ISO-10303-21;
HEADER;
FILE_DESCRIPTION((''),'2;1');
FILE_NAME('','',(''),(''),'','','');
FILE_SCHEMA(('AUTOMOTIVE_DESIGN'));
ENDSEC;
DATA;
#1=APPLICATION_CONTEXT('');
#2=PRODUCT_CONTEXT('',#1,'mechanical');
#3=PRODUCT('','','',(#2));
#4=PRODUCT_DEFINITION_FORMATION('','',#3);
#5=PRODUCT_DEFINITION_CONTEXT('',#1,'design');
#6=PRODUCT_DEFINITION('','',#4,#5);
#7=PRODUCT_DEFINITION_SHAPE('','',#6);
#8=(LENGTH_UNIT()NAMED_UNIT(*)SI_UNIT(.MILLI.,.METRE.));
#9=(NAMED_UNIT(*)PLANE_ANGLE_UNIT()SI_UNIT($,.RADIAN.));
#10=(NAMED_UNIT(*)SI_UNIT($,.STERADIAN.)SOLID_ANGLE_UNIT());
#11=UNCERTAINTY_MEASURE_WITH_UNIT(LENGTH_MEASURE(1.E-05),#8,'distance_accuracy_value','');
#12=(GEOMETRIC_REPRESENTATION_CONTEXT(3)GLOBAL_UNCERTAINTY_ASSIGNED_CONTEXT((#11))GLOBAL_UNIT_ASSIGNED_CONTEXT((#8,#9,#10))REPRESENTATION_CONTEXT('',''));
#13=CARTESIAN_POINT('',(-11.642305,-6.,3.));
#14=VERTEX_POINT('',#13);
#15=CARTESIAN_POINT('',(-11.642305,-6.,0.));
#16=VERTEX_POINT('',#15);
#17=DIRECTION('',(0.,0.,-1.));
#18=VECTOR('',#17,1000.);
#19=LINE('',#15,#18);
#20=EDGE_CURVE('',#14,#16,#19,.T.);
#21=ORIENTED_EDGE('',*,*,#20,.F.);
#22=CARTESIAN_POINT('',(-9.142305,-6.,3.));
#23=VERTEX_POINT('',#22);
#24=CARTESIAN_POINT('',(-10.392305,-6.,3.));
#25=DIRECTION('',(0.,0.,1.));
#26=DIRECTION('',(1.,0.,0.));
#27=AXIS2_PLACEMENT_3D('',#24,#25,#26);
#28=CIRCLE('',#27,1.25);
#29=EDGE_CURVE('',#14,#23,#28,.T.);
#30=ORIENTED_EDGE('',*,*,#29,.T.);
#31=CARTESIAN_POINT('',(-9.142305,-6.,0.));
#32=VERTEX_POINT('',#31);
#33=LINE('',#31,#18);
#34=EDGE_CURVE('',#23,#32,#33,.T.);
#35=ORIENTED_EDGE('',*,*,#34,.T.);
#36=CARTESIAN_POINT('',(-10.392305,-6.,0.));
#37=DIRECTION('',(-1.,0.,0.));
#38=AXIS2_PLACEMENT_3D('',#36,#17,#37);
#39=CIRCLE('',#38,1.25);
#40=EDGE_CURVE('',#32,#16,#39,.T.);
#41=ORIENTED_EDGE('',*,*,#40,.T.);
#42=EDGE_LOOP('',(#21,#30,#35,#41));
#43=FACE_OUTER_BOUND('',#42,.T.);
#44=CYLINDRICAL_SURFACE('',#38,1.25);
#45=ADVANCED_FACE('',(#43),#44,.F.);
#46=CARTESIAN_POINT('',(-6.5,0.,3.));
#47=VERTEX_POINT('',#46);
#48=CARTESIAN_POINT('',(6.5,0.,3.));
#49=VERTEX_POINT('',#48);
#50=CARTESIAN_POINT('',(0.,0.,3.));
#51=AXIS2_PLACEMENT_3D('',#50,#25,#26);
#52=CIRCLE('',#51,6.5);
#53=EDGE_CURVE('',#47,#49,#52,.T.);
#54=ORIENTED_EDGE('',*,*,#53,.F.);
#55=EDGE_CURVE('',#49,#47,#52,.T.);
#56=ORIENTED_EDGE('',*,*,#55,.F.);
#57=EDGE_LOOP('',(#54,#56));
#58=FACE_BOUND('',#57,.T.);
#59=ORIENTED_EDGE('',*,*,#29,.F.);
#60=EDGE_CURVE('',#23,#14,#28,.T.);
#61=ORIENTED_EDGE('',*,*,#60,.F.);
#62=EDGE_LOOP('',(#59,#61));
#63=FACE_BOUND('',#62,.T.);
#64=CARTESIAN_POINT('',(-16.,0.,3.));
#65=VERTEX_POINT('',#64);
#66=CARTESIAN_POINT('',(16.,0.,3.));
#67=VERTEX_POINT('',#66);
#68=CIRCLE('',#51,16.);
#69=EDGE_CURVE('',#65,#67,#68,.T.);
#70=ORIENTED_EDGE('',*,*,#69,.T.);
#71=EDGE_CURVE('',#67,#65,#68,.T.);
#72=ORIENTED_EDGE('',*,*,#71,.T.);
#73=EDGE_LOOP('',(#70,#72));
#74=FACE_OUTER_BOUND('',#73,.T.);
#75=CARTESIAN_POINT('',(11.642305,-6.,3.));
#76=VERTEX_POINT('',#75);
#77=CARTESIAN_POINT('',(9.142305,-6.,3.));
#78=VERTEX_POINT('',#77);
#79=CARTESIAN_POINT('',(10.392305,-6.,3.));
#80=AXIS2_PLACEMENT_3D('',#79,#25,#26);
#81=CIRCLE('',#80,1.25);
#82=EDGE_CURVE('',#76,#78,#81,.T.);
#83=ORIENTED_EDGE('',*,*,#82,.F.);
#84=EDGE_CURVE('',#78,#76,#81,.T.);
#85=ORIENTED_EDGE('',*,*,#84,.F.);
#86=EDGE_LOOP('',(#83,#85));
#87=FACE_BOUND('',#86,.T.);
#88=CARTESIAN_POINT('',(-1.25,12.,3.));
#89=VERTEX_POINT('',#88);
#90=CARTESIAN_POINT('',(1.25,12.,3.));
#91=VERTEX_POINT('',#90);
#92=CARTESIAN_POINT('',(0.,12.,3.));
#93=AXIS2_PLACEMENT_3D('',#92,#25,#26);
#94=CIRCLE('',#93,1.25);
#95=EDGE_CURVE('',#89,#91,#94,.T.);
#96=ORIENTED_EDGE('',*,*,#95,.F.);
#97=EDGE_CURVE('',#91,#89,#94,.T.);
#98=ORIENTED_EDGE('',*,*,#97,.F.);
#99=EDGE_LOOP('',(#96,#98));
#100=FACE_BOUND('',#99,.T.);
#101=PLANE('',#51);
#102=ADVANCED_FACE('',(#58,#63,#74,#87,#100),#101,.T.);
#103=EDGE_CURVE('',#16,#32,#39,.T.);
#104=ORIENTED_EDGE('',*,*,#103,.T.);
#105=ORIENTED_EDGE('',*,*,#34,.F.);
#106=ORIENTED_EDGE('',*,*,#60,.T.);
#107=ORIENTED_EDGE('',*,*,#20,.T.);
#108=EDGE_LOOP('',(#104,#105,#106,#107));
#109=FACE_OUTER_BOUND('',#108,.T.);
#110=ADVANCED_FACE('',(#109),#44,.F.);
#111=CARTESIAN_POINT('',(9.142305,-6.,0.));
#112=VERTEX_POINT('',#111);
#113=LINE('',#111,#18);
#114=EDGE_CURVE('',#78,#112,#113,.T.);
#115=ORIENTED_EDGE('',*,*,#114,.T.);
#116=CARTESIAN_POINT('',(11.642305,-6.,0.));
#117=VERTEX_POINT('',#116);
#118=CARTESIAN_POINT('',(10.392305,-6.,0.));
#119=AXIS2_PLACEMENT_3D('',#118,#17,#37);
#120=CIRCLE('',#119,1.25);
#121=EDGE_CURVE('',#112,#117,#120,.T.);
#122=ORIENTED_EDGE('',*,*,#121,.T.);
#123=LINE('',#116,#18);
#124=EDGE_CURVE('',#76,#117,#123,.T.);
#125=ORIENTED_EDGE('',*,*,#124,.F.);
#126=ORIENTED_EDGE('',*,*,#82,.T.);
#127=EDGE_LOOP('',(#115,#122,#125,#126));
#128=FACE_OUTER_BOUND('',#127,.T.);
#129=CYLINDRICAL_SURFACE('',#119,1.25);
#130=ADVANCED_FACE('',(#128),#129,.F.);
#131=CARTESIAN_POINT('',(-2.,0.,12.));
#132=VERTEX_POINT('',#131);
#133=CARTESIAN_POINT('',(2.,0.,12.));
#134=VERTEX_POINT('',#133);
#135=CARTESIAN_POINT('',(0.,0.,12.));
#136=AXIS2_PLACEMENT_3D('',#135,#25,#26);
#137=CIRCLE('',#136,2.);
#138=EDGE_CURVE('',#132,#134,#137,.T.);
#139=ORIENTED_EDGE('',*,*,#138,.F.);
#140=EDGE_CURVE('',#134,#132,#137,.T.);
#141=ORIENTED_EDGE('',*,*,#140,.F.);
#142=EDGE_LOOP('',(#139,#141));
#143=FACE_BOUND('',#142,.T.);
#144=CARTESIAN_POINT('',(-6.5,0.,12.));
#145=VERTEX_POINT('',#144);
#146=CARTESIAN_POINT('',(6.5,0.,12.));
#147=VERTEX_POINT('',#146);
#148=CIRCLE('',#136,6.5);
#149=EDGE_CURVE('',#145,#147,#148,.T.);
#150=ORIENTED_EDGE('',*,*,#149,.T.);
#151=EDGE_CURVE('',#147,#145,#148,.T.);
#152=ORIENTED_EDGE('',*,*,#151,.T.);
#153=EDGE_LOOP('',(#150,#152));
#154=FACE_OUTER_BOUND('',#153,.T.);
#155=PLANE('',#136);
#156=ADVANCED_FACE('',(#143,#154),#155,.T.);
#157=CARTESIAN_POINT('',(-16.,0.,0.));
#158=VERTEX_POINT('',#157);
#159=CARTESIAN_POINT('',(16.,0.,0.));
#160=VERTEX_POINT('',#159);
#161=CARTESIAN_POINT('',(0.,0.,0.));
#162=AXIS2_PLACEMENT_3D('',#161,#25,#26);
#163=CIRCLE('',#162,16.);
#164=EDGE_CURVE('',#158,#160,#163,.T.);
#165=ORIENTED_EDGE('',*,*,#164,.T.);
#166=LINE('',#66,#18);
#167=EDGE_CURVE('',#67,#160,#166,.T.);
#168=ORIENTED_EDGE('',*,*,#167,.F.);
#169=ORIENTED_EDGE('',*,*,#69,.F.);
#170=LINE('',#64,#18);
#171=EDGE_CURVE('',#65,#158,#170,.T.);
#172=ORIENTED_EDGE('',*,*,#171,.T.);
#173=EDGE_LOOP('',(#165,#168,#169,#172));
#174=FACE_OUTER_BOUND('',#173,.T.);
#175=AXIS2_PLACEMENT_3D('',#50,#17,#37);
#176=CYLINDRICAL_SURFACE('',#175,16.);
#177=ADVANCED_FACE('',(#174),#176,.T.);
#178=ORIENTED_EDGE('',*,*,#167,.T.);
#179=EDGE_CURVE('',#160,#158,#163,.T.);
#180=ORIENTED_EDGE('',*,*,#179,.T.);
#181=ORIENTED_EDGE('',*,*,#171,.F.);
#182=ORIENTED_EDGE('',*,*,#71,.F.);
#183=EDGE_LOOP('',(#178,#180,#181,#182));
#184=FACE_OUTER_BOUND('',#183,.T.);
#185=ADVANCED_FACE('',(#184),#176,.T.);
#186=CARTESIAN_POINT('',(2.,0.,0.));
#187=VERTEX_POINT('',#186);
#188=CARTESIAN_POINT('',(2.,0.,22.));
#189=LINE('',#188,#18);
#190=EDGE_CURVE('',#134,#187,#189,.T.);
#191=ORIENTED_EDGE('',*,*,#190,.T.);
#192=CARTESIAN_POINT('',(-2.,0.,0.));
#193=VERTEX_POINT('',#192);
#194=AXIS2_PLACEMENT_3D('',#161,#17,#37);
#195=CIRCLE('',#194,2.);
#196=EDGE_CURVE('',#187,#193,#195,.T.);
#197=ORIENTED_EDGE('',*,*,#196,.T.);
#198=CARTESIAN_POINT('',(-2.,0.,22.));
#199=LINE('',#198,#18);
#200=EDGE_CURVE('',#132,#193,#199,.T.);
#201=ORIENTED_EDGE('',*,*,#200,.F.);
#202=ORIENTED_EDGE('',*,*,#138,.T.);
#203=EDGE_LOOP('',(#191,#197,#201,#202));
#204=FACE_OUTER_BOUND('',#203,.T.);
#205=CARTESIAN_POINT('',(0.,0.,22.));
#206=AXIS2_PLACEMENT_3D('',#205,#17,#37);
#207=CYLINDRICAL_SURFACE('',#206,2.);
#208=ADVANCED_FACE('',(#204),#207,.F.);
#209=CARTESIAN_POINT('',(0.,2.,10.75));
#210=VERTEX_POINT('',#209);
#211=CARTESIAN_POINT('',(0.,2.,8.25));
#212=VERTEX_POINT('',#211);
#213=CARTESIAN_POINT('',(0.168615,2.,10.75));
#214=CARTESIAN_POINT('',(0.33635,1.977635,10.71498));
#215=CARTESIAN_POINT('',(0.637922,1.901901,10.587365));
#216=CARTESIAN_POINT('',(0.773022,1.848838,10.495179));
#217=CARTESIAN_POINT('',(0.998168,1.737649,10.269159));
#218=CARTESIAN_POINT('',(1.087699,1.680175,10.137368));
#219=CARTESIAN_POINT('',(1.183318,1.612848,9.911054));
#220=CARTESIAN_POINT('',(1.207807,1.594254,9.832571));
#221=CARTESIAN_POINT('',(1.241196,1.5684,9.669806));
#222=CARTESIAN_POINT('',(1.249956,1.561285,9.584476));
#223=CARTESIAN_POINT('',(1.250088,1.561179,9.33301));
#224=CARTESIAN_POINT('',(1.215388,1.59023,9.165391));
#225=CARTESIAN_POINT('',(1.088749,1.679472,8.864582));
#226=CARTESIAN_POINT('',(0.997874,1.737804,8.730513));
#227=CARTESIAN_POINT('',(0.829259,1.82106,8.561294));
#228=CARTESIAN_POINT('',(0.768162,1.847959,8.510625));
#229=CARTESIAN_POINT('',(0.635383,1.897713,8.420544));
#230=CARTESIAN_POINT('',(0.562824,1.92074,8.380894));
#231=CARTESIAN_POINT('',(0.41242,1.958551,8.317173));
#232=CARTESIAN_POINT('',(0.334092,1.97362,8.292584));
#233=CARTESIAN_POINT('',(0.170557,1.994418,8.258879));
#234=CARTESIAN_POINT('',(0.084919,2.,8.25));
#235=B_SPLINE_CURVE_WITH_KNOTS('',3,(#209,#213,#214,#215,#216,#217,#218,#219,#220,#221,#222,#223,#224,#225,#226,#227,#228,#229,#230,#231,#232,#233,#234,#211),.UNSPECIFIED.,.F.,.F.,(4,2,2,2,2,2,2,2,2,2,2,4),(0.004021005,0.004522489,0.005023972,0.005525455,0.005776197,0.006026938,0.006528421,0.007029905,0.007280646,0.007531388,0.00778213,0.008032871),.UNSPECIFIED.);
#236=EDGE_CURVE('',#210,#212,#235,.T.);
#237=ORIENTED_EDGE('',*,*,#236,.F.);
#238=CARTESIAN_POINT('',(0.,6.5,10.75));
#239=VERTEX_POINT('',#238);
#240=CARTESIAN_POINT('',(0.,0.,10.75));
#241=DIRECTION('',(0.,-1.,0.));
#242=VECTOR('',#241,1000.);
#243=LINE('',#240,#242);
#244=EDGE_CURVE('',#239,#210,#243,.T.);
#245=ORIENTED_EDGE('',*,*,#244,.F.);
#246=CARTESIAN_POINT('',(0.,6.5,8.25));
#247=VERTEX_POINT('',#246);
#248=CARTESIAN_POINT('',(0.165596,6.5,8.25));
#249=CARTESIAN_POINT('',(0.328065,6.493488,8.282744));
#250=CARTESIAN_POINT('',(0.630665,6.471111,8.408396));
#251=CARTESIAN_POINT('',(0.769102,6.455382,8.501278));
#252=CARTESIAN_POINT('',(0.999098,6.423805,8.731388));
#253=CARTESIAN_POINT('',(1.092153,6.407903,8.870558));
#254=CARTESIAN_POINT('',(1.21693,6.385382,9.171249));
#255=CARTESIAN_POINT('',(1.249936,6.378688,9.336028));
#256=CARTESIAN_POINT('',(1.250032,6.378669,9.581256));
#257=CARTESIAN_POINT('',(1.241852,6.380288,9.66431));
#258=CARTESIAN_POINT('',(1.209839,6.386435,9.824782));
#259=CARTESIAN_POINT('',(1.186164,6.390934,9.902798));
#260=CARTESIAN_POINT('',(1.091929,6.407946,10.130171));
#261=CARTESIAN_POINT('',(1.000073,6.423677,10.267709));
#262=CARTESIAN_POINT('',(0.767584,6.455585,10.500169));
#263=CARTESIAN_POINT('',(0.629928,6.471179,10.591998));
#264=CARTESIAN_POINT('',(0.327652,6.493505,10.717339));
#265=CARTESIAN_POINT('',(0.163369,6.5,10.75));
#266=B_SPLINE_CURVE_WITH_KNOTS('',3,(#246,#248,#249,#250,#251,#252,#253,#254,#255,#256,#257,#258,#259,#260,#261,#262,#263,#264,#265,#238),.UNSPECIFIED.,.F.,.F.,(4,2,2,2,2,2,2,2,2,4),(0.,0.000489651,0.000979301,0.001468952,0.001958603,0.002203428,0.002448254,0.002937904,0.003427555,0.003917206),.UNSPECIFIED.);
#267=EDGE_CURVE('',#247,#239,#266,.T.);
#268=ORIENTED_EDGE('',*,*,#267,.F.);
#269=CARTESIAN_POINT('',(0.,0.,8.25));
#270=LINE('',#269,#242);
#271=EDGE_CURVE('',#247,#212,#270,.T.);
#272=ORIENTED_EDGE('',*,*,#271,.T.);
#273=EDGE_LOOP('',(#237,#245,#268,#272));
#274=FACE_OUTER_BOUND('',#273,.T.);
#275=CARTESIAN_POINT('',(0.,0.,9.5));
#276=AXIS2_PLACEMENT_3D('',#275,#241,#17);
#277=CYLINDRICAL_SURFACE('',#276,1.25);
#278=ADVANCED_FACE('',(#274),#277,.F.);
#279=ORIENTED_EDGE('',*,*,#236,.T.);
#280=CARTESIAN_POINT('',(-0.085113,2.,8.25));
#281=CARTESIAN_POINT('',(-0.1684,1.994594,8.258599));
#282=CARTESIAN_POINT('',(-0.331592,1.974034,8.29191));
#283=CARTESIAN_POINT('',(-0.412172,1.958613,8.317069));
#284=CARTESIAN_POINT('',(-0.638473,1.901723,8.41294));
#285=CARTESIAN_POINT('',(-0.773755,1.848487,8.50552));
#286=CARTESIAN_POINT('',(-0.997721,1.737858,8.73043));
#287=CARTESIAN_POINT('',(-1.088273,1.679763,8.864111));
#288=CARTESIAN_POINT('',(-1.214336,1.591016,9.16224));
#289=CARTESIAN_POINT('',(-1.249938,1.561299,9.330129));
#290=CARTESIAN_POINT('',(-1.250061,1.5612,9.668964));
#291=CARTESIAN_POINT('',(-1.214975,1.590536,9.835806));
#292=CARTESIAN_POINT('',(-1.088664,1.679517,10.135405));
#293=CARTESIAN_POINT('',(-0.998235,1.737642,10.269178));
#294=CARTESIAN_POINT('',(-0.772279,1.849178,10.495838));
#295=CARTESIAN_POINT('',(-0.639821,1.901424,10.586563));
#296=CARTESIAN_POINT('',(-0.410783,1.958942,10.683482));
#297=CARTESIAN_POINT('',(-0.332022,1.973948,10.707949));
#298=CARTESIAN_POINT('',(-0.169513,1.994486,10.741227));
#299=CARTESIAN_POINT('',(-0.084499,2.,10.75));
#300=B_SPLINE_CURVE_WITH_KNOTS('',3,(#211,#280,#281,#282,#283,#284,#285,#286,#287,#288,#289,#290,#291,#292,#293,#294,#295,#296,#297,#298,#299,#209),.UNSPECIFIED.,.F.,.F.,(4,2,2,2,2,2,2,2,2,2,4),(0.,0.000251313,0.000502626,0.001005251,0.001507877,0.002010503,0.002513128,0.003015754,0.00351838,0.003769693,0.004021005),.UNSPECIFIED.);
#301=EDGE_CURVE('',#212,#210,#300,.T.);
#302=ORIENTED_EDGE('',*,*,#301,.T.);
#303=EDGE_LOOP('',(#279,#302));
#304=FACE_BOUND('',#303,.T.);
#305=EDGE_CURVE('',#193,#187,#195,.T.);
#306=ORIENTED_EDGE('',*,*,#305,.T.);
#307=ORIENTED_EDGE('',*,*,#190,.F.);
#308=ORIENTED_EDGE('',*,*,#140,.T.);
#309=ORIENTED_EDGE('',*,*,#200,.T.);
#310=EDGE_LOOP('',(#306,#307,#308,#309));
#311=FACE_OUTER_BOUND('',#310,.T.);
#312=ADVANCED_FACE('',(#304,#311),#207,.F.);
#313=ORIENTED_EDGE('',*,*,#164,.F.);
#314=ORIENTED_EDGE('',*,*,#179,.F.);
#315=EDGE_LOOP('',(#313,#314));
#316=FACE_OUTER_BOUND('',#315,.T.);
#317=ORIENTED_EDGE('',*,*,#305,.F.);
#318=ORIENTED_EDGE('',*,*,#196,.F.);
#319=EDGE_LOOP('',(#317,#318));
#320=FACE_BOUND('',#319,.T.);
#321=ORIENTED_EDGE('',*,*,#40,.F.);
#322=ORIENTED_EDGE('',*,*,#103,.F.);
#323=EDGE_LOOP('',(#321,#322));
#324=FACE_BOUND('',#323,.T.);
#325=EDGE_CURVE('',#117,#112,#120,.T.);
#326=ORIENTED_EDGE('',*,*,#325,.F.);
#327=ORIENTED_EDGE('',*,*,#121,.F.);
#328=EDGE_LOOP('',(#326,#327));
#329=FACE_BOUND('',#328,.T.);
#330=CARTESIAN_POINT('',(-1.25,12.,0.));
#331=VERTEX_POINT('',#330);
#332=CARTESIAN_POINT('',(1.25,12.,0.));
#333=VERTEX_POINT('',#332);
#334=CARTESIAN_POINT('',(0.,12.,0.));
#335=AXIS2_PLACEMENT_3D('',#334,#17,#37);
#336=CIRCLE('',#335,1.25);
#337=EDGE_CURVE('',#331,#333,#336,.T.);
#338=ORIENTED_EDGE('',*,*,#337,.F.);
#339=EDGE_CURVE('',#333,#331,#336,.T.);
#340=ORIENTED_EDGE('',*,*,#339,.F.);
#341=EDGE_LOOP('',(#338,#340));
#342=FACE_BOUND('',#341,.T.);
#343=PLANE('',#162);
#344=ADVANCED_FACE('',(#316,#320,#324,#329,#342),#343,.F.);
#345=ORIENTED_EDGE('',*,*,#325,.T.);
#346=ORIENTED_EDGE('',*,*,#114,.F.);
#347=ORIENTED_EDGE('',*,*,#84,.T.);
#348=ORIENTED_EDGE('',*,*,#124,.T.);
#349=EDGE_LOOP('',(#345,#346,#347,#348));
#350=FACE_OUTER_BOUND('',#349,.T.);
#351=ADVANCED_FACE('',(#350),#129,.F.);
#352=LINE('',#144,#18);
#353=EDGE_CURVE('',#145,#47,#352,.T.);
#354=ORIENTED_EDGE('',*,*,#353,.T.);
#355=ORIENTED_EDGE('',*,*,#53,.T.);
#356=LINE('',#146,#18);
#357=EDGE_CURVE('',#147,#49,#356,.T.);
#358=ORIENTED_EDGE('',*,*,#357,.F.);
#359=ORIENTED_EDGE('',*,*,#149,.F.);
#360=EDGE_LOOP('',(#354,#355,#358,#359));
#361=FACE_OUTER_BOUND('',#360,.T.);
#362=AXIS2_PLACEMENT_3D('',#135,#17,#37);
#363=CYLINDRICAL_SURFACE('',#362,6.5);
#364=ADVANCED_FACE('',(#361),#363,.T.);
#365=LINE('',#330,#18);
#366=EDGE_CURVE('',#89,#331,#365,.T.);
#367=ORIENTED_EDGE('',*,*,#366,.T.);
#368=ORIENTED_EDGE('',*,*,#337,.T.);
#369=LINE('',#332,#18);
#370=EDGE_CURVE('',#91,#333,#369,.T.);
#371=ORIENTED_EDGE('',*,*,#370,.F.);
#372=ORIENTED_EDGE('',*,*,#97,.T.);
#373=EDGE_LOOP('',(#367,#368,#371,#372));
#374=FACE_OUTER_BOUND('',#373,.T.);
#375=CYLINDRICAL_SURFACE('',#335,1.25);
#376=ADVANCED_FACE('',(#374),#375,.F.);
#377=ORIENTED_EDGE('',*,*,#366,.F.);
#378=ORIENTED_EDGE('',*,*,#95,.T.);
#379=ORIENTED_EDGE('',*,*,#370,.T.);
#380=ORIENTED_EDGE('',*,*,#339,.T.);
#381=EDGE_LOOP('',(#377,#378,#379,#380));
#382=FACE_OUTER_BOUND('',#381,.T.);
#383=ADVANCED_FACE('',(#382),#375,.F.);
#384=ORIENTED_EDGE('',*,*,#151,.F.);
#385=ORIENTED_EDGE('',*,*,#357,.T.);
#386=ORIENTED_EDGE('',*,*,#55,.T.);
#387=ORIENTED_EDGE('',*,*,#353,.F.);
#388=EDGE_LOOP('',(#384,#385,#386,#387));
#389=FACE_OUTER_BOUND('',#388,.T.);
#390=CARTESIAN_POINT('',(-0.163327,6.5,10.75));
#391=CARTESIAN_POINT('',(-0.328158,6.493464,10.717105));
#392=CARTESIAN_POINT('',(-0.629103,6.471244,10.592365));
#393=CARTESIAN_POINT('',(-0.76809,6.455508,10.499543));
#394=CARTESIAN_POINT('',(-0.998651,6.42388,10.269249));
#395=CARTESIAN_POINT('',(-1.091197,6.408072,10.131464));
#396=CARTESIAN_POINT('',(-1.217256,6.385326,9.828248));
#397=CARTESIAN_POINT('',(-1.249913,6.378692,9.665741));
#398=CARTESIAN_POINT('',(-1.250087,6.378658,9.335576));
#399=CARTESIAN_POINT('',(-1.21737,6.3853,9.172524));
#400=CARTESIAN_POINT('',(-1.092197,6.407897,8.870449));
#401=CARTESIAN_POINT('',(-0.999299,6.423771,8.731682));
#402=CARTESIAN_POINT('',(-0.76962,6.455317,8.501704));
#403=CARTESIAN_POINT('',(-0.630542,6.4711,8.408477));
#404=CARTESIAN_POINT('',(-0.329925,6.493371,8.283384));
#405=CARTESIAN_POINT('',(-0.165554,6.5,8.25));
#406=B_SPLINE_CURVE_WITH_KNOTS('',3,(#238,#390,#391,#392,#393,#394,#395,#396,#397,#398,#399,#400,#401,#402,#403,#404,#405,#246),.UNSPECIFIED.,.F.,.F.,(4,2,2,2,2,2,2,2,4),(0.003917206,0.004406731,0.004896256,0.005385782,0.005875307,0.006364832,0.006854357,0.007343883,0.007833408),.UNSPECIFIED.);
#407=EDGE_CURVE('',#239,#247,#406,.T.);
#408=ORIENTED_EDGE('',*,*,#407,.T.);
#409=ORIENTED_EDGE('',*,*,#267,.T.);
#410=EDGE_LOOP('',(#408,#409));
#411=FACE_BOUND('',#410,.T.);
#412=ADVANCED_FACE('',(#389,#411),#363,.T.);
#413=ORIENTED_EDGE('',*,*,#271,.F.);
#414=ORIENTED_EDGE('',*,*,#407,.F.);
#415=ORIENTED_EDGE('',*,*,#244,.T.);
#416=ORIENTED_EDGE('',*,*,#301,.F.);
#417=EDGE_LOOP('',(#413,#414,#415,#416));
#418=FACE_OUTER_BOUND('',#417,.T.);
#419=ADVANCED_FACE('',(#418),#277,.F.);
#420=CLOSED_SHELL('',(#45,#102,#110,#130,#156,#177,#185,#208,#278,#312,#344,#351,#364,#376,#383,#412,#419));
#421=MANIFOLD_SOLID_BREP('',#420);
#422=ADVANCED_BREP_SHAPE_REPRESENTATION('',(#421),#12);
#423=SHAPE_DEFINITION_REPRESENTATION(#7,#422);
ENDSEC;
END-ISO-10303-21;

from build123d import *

# Parameters (mm, degrees)
SKETCH1_R             = 16
BOSS_EXTRUDE1_DEPTH   = 3
SKETCH2_R             = 6.5
BOSS_EXTRUDE2_DEPTH   = 9
SKETCH3_R             = 2
CUT_EXTRUDE1_DEPTH    = 22
SKETCH4_R             = 1
CUT_EXTRUDE2_DEPTH    = 10
M3_TAPPED_HOLE6_D     = 2.5
M3_TAPPED_HOLE6_DEPTH = 12


with BuildPart() as part:
    # Sketch1 → Boss-Extrude1 (new body)
    with BuildSketch(Plane.XY):
        Circle(SKETCH1_R)
    extrude(amount=BOSS_EXTRUDE1_DEPTH)

    # Sketch2 → Boss-Extrude2 (add)
    with BuildSketch(Plane.XY.offset(3)):
        Circle(SKETCH2_R)
    extrude(amount=BOSS_EXTRUDE2_DEPTH)

    # Sketch3 → Cut-Extrude1 (cut)
    with BuildSketch(Plane(origin=(0, 0, 0), x_dir=(-1, 0, 0), z_dir=(0, 0, -1))):
        Circle(SKETCH3_R)
    extrude(amount=-CUT_EXTRUDE1_DEPTH, mode=Mode.SUBTRACT)

    # Sketch16 → M3 Tapped Hole5 (revolve, cut)
    with BuildSketch(Plane(origin=(0, 0, 9.5), x_dir=(0, 0, -1), z_dir=(1, 0, 0))):
        Polygon((0, 0), (0, 8.251075774), (1.25, 7.5), (1.25, 0), align=None)
    revolve(axis=Axis((0, -6.35, 9.5), (0, 1, 0)), mode=Mode.SUBTRACT)

    # Sketch4 → Cut-Extrude2 (cut)
    with BuildSketch(Plane(origin=(0, 0, 0), x_dir=(-1, 0, 0), z_dir=(0, 0, -1))):
        with Locations((0, 12)):
            Circle(SKETCH4_R)
        with Locations((10.392304845, -6)):
            Circle(SKETCH4_R)
        with Locations((-10.392304845, -6)):
            Circle(SKETCH4_R)
    extrude(amount=-CUT_EXTRUDE2_DEPTH, mode=Mode.SUBTRACT)

    # M3 Tapped Hole6
    with Locations(Plane(origin=(0, 0, 0), x_dir=(-1, 0, 0), z_dir=(0, 0, -1))):
        with Locations((0, 12), (-10.392304845, -6), (10.392304845, -6)):
            Hole(M3_TAPPED_HOLE6_D / 2, depth=M3_TAPPED_HOLE6_DEPTH)


solid = part.part
